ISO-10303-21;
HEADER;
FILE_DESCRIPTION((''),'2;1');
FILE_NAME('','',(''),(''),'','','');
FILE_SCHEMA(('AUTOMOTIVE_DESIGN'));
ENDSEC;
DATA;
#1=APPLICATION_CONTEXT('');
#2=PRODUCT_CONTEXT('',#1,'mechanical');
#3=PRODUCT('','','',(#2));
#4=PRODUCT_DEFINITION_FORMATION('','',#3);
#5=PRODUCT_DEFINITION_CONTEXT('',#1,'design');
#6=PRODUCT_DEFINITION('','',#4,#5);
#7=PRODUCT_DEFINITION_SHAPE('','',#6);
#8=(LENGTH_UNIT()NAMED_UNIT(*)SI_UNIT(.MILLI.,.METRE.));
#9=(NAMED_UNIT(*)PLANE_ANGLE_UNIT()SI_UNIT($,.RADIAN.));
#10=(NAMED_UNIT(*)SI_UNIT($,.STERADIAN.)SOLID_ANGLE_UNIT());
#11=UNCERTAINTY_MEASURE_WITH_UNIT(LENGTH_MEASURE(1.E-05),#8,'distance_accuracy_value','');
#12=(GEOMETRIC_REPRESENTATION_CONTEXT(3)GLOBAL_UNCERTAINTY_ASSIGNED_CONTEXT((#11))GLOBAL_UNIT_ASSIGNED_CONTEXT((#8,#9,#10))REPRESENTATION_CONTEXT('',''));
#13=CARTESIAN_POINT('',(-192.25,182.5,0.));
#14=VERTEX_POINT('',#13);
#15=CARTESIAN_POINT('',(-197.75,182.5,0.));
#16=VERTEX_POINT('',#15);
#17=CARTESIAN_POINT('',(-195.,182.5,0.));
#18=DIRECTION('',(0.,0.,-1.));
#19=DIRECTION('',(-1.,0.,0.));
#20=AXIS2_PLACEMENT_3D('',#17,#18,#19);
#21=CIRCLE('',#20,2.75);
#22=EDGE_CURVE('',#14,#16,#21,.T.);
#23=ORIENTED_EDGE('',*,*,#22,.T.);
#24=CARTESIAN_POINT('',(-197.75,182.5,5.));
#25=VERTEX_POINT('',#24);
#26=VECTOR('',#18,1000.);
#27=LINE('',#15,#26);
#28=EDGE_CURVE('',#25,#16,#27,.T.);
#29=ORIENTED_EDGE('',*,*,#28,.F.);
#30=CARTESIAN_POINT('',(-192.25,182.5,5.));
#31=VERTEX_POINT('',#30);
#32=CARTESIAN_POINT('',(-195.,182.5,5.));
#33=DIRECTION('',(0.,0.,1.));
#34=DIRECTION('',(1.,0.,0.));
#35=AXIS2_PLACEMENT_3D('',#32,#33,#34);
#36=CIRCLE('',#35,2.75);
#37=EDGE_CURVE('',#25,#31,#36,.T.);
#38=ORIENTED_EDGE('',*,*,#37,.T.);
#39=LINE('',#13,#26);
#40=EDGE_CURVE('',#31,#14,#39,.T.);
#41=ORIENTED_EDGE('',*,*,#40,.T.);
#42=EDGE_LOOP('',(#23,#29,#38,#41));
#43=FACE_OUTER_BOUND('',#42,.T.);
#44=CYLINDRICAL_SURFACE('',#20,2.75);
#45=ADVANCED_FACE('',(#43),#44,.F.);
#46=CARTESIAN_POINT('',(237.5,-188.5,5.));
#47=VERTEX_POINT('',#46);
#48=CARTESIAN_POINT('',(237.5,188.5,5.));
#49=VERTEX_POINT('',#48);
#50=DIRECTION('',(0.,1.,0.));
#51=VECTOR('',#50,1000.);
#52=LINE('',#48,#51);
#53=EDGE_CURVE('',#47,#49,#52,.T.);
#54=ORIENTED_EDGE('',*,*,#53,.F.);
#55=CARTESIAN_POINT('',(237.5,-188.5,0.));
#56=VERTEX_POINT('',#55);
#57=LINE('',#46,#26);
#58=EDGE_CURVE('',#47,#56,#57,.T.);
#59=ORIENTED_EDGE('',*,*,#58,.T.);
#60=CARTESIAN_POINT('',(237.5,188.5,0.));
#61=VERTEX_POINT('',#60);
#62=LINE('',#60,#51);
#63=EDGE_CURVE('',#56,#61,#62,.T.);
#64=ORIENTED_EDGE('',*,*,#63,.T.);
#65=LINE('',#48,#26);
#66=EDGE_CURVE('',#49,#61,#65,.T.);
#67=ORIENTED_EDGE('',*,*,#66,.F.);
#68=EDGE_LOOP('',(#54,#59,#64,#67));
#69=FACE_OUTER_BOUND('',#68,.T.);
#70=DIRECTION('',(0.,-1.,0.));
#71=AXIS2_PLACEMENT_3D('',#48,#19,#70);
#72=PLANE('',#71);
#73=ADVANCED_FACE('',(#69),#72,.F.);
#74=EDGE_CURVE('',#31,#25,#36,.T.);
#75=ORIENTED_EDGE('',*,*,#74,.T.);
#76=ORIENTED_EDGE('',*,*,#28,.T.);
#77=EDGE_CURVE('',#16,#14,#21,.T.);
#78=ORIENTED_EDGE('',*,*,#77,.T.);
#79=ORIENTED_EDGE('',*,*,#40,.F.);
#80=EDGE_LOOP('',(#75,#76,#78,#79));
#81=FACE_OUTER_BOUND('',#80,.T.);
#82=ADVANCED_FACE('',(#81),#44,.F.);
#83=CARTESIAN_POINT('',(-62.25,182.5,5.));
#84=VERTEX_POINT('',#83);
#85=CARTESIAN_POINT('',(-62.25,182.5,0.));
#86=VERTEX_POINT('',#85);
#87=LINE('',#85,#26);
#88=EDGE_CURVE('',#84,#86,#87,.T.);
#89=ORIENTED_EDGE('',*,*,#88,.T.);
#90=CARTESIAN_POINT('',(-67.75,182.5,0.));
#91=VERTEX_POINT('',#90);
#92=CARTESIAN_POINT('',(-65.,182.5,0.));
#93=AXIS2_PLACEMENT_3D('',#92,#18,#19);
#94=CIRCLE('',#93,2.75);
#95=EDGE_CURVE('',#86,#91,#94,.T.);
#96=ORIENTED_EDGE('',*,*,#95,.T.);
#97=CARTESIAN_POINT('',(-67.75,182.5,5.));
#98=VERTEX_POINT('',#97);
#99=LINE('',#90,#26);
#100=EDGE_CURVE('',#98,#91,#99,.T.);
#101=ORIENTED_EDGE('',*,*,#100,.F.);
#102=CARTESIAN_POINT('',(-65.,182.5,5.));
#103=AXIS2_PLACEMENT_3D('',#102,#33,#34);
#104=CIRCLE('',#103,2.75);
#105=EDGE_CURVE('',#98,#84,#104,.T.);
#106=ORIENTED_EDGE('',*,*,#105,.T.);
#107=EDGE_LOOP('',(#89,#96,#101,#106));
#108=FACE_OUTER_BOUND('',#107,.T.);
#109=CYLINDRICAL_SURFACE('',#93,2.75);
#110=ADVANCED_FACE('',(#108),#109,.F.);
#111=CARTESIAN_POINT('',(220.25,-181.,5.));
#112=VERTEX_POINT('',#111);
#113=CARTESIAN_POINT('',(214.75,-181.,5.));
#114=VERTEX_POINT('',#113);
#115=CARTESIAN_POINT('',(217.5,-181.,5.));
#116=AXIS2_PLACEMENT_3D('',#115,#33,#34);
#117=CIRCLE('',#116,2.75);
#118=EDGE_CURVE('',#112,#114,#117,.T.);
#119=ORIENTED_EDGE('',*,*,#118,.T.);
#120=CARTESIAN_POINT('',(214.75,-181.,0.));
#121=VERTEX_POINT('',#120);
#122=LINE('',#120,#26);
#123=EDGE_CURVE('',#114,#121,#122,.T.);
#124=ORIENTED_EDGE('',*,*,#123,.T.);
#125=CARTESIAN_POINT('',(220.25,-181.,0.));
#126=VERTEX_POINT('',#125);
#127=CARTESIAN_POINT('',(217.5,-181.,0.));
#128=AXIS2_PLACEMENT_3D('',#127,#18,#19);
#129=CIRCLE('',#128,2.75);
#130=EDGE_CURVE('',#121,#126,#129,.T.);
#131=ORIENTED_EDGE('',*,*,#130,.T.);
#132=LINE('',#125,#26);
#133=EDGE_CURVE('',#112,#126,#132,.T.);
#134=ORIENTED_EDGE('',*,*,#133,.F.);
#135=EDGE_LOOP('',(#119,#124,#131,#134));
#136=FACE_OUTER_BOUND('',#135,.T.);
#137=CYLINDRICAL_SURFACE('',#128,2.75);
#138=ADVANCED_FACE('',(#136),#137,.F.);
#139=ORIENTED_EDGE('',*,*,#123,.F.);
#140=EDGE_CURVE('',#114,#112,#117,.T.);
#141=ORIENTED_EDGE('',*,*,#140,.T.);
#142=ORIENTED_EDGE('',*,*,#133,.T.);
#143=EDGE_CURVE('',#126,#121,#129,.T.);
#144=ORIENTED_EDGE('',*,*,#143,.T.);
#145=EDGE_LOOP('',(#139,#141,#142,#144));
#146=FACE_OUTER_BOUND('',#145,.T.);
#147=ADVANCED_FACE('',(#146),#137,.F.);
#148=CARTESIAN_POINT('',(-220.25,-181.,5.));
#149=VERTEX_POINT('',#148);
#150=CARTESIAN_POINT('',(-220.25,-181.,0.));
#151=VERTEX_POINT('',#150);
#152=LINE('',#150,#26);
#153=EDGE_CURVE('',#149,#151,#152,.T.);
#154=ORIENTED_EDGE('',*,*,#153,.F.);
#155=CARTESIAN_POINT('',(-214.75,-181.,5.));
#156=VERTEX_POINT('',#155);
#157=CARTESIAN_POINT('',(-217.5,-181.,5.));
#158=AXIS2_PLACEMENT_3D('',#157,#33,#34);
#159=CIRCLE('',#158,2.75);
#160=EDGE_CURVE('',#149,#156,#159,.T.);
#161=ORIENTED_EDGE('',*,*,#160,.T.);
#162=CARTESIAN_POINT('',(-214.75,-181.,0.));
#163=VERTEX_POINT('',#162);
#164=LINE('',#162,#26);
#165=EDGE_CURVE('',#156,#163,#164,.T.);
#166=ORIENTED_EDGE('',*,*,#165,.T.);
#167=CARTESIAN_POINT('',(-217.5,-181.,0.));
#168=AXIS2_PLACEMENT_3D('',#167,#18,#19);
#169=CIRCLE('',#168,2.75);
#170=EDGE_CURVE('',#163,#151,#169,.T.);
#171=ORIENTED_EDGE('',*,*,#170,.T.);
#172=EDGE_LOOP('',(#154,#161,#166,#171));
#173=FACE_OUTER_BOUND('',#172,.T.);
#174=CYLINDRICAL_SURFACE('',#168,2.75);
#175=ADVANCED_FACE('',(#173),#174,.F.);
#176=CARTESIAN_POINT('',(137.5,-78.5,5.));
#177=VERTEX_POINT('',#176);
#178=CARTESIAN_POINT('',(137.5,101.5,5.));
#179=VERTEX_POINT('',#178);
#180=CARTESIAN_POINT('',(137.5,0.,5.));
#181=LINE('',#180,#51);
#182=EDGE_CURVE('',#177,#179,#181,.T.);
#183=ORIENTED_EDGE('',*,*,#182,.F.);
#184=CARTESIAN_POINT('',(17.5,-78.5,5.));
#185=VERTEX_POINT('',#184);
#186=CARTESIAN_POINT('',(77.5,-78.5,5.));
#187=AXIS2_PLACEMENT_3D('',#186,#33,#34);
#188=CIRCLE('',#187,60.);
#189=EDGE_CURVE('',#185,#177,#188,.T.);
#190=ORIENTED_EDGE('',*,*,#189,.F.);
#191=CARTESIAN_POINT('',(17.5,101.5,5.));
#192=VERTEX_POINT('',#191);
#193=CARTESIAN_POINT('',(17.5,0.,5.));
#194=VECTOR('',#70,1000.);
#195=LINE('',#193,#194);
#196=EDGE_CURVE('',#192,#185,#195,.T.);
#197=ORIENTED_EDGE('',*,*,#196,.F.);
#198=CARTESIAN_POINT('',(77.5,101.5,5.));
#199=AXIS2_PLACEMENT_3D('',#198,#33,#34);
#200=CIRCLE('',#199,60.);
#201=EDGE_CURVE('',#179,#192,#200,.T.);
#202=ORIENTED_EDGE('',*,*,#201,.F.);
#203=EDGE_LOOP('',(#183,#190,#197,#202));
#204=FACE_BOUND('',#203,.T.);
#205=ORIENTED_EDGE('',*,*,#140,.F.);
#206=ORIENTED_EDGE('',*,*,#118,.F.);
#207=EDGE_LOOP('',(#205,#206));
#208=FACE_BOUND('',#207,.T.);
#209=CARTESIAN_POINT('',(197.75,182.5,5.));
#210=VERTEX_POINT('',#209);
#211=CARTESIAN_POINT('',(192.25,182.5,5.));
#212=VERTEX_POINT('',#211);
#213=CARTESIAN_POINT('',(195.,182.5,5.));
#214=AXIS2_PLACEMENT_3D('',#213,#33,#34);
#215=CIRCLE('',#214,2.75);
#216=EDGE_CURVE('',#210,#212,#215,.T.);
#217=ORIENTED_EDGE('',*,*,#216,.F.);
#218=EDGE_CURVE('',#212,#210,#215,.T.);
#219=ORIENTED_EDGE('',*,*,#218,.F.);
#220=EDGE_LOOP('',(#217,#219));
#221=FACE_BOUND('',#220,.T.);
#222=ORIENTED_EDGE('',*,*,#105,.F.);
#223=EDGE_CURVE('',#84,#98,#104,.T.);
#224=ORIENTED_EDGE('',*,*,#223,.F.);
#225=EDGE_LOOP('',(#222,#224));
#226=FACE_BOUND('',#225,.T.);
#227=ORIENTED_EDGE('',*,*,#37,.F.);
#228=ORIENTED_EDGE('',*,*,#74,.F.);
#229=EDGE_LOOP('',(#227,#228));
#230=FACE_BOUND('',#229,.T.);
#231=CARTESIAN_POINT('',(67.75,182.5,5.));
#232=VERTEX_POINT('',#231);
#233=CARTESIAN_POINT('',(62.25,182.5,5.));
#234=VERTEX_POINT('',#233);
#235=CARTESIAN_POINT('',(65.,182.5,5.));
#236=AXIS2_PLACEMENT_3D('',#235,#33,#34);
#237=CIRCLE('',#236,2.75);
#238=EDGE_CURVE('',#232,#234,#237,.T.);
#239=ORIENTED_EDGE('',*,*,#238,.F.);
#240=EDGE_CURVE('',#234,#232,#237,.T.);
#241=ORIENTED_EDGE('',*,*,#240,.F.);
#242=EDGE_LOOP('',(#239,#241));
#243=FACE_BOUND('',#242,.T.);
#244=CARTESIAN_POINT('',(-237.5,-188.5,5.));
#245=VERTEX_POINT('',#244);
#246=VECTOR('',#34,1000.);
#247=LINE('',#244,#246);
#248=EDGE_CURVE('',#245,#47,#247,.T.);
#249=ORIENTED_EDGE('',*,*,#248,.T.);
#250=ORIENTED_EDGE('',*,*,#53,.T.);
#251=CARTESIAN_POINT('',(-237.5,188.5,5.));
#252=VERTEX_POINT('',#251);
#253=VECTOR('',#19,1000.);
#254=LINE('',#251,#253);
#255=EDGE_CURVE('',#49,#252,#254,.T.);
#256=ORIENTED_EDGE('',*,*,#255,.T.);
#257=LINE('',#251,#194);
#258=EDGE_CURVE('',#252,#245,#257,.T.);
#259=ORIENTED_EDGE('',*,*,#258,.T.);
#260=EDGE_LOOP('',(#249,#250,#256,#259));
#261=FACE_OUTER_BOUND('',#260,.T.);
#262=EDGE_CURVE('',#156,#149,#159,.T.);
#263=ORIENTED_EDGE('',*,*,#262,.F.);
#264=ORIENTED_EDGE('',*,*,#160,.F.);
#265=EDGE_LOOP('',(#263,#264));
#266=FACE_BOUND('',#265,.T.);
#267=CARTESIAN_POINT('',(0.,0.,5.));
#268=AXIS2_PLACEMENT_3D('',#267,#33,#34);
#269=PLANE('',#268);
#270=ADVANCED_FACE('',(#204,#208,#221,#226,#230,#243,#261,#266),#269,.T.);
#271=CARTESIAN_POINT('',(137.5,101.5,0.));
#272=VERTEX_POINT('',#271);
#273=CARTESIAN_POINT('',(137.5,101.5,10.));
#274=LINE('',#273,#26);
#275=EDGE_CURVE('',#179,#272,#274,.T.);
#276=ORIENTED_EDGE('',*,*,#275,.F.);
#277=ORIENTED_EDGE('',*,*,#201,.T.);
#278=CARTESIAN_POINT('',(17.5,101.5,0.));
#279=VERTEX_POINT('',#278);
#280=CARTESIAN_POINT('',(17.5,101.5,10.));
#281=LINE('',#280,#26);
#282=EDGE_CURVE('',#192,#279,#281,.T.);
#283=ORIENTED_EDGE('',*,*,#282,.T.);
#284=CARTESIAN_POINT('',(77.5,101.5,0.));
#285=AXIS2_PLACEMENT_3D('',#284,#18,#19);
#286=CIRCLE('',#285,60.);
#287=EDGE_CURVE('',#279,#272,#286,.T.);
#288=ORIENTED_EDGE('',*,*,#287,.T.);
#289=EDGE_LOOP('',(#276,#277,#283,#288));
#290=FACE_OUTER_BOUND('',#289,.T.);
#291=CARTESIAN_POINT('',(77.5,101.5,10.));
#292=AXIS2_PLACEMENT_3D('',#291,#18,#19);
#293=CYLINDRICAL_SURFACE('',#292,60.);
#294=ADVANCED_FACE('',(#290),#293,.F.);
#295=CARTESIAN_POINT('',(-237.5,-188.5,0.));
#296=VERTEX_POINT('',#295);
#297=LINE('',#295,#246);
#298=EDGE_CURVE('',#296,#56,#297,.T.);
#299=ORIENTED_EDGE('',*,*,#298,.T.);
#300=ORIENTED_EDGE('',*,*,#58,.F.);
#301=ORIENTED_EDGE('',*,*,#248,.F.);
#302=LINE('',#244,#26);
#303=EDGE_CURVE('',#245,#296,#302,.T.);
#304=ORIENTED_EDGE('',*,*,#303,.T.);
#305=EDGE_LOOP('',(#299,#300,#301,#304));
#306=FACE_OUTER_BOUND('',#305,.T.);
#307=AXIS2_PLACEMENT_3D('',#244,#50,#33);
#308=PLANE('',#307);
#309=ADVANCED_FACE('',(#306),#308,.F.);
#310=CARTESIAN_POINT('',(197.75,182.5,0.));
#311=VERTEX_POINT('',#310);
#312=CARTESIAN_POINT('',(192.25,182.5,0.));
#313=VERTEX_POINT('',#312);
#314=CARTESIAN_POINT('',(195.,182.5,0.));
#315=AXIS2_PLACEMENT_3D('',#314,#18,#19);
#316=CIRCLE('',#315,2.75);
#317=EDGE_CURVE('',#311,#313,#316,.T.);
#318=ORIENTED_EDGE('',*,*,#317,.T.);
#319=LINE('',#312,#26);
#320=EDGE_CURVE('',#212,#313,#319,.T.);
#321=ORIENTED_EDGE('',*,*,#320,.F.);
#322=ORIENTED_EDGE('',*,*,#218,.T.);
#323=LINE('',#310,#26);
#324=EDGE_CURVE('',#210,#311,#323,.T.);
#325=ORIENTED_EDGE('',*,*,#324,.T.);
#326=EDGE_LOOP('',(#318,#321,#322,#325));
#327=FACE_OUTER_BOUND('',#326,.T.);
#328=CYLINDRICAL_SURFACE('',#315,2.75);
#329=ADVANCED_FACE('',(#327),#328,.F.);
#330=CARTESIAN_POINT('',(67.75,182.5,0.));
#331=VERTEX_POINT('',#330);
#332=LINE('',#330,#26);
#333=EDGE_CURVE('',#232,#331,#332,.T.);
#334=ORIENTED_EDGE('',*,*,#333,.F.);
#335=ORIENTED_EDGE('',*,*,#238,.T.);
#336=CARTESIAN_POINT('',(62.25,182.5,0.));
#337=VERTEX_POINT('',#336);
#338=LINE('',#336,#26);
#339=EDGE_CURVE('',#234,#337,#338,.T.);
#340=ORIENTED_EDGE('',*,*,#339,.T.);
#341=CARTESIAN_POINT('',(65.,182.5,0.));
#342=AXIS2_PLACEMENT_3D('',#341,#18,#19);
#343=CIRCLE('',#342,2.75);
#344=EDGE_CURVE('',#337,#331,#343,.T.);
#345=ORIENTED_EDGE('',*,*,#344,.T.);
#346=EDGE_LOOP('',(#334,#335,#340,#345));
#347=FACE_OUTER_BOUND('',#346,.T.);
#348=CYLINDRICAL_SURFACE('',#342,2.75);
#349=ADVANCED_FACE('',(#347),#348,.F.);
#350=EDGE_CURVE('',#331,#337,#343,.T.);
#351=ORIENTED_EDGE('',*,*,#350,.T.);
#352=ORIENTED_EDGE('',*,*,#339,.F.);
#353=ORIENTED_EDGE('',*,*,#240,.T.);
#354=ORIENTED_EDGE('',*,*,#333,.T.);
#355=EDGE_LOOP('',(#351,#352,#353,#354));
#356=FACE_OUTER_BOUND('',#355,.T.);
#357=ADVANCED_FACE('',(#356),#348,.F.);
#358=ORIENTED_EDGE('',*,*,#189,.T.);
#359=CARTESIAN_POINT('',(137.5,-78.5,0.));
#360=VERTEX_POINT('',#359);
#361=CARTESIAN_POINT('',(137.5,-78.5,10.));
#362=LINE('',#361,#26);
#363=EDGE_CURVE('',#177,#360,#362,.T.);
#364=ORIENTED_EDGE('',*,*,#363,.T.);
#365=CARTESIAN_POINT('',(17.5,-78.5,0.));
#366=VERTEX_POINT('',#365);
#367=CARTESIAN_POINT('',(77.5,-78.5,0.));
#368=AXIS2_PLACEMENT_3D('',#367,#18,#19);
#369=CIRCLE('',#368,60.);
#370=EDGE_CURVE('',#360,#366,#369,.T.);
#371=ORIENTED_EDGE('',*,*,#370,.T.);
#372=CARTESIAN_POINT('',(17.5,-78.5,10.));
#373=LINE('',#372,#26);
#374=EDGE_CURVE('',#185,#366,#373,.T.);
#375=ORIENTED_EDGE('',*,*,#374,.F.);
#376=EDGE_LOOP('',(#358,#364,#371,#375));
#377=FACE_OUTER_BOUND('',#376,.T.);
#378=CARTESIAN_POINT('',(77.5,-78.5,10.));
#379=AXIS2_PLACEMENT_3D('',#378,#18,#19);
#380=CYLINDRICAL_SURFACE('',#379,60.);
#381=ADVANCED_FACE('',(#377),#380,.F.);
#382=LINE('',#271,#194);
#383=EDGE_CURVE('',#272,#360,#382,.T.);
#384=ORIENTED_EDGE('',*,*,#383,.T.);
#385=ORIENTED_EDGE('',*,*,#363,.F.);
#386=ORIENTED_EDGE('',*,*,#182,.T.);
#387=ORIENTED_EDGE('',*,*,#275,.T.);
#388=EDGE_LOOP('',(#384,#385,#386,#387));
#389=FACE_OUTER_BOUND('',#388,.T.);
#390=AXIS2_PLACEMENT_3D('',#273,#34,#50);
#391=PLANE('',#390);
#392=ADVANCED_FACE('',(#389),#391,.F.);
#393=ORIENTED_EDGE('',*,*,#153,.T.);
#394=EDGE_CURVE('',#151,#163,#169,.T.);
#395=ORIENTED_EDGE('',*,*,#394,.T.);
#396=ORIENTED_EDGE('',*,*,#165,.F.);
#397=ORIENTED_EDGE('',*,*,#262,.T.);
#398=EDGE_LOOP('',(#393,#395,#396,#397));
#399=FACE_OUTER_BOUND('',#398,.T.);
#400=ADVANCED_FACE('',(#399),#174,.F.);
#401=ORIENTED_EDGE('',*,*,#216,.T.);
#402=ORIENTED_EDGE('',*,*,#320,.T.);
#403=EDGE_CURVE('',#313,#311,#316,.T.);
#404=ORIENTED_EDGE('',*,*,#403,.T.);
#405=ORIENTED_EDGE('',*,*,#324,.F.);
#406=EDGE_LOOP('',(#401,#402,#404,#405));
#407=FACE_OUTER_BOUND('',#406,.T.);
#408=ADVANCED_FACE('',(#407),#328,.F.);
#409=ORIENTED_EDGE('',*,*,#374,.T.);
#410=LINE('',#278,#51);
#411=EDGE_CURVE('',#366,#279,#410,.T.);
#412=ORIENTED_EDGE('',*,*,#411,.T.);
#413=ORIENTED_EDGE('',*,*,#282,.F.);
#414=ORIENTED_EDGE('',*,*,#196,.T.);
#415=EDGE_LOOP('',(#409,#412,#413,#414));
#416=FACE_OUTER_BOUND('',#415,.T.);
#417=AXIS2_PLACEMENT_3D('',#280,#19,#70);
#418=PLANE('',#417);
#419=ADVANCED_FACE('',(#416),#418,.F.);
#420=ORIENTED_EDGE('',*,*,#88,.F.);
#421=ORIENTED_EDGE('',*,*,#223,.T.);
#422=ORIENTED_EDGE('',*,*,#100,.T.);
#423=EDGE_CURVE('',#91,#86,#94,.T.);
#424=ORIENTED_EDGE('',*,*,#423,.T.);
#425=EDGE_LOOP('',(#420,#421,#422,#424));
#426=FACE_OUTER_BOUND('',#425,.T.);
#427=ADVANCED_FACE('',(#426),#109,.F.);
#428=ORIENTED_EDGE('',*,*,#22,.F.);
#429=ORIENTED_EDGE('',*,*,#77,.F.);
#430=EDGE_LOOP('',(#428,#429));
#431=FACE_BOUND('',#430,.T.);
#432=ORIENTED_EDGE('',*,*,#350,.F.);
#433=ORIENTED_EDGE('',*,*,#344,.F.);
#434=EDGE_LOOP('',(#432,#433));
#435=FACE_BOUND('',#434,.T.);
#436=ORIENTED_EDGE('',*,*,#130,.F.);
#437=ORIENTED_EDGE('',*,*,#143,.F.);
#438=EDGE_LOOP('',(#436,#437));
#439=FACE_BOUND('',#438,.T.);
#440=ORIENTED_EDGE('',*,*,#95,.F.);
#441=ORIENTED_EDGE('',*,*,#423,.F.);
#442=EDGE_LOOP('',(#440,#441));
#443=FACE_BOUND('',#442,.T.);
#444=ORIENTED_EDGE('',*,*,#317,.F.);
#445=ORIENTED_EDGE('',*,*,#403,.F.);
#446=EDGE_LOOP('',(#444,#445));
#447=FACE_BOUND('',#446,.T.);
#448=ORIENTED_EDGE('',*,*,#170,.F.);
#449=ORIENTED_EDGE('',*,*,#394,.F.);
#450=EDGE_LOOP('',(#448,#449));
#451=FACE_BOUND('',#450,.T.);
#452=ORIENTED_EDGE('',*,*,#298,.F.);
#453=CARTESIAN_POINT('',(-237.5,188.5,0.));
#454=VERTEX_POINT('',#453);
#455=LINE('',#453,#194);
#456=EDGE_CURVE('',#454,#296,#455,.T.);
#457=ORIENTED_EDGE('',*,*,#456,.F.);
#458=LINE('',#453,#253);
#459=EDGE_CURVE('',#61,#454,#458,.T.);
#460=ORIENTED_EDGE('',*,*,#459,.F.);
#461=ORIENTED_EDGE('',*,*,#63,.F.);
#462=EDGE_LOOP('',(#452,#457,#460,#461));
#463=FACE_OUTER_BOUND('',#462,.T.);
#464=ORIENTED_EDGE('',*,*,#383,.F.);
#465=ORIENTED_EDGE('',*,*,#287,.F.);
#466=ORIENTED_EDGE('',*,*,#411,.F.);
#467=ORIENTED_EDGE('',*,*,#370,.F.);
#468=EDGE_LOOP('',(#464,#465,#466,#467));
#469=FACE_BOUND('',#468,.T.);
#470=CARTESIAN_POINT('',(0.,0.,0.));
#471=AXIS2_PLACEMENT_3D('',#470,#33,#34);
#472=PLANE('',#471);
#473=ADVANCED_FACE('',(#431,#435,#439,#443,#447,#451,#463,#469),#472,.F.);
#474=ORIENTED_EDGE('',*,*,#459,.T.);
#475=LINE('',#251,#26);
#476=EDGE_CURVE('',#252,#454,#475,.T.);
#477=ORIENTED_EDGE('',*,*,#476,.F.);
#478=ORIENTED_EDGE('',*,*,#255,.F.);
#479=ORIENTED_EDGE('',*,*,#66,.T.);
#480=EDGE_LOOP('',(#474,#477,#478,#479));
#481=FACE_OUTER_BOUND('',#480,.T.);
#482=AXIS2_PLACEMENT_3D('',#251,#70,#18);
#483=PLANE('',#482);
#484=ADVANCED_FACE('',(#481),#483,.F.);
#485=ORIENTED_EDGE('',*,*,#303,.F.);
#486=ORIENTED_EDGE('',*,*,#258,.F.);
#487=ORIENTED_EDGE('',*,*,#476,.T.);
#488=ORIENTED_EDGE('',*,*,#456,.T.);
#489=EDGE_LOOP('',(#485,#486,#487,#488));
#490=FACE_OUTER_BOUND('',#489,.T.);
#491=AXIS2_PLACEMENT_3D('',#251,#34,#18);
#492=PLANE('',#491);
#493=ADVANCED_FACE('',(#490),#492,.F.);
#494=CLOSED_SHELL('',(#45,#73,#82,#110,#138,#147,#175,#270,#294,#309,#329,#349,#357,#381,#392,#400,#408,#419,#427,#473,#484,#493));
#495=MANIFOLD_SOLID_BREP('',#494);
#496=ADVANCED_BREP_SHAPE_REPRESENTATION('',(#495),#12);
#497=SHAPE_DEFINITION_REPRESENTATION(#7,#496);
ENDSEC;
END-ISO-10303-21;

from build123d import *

# Parameters (mm, degrees)
SKETCH1_W            = 475
SKETCH1_H            = 377
BOSS_EXTRUDE1_DEPTH  = 5
M5_CLEARANCE_HOLE1_D = 5.5
CUT_EXTRUDE1_DEPTH   = 10


with BuildPart() as part:
    # Sketch1 → Boss-Extrude1 (new body)
    with BuildSketch(Plane.XY):
        Rectangle(SKETCH1_W, SKETCH1_H)
    extrude(amount=BOSS_EXTRUDE1_DEPTH)

    # M5 Clearance Hole1 (through all)
    with Locations(Plane(origin=(0, 0, 0), x_dir=(-1, 0, 0), z_dir=(0, 0, -1))):
        with Locations((-195, 182.5), (-65, 182.5), (65, 182.5), (195, 182.5), (217.5, -181), (-217.5, -181)):
            Hole(M5_CLEARANCE_HOLE1_D / 2)

    # Sketch3 → Cut-Extrude1 (cut)
    with BuildSketch(Plane(origin=(0, 0, 0), x_dir=(-1, 0, 0), z_dir=(0, 0, -1))):
        with BuildLine():
            Line((-17.5, 101.5), (-17.5, -78.5))
            ThreePointArc((-17.5, -78.5), (-77.5, -138.5), (-137.5, -78.5))
            Line((-137.5, -78.5), (-137.5, 101.5))
            ThreePointArc((-137.5, 101.5), (-77.5, 161.5), (-17.5, 101.5))
        make_face()
    extrude(amount=-CUT_EXTRUDE1_DEPTH, mode=Mode.SUBTRACT)


solid = part.part
